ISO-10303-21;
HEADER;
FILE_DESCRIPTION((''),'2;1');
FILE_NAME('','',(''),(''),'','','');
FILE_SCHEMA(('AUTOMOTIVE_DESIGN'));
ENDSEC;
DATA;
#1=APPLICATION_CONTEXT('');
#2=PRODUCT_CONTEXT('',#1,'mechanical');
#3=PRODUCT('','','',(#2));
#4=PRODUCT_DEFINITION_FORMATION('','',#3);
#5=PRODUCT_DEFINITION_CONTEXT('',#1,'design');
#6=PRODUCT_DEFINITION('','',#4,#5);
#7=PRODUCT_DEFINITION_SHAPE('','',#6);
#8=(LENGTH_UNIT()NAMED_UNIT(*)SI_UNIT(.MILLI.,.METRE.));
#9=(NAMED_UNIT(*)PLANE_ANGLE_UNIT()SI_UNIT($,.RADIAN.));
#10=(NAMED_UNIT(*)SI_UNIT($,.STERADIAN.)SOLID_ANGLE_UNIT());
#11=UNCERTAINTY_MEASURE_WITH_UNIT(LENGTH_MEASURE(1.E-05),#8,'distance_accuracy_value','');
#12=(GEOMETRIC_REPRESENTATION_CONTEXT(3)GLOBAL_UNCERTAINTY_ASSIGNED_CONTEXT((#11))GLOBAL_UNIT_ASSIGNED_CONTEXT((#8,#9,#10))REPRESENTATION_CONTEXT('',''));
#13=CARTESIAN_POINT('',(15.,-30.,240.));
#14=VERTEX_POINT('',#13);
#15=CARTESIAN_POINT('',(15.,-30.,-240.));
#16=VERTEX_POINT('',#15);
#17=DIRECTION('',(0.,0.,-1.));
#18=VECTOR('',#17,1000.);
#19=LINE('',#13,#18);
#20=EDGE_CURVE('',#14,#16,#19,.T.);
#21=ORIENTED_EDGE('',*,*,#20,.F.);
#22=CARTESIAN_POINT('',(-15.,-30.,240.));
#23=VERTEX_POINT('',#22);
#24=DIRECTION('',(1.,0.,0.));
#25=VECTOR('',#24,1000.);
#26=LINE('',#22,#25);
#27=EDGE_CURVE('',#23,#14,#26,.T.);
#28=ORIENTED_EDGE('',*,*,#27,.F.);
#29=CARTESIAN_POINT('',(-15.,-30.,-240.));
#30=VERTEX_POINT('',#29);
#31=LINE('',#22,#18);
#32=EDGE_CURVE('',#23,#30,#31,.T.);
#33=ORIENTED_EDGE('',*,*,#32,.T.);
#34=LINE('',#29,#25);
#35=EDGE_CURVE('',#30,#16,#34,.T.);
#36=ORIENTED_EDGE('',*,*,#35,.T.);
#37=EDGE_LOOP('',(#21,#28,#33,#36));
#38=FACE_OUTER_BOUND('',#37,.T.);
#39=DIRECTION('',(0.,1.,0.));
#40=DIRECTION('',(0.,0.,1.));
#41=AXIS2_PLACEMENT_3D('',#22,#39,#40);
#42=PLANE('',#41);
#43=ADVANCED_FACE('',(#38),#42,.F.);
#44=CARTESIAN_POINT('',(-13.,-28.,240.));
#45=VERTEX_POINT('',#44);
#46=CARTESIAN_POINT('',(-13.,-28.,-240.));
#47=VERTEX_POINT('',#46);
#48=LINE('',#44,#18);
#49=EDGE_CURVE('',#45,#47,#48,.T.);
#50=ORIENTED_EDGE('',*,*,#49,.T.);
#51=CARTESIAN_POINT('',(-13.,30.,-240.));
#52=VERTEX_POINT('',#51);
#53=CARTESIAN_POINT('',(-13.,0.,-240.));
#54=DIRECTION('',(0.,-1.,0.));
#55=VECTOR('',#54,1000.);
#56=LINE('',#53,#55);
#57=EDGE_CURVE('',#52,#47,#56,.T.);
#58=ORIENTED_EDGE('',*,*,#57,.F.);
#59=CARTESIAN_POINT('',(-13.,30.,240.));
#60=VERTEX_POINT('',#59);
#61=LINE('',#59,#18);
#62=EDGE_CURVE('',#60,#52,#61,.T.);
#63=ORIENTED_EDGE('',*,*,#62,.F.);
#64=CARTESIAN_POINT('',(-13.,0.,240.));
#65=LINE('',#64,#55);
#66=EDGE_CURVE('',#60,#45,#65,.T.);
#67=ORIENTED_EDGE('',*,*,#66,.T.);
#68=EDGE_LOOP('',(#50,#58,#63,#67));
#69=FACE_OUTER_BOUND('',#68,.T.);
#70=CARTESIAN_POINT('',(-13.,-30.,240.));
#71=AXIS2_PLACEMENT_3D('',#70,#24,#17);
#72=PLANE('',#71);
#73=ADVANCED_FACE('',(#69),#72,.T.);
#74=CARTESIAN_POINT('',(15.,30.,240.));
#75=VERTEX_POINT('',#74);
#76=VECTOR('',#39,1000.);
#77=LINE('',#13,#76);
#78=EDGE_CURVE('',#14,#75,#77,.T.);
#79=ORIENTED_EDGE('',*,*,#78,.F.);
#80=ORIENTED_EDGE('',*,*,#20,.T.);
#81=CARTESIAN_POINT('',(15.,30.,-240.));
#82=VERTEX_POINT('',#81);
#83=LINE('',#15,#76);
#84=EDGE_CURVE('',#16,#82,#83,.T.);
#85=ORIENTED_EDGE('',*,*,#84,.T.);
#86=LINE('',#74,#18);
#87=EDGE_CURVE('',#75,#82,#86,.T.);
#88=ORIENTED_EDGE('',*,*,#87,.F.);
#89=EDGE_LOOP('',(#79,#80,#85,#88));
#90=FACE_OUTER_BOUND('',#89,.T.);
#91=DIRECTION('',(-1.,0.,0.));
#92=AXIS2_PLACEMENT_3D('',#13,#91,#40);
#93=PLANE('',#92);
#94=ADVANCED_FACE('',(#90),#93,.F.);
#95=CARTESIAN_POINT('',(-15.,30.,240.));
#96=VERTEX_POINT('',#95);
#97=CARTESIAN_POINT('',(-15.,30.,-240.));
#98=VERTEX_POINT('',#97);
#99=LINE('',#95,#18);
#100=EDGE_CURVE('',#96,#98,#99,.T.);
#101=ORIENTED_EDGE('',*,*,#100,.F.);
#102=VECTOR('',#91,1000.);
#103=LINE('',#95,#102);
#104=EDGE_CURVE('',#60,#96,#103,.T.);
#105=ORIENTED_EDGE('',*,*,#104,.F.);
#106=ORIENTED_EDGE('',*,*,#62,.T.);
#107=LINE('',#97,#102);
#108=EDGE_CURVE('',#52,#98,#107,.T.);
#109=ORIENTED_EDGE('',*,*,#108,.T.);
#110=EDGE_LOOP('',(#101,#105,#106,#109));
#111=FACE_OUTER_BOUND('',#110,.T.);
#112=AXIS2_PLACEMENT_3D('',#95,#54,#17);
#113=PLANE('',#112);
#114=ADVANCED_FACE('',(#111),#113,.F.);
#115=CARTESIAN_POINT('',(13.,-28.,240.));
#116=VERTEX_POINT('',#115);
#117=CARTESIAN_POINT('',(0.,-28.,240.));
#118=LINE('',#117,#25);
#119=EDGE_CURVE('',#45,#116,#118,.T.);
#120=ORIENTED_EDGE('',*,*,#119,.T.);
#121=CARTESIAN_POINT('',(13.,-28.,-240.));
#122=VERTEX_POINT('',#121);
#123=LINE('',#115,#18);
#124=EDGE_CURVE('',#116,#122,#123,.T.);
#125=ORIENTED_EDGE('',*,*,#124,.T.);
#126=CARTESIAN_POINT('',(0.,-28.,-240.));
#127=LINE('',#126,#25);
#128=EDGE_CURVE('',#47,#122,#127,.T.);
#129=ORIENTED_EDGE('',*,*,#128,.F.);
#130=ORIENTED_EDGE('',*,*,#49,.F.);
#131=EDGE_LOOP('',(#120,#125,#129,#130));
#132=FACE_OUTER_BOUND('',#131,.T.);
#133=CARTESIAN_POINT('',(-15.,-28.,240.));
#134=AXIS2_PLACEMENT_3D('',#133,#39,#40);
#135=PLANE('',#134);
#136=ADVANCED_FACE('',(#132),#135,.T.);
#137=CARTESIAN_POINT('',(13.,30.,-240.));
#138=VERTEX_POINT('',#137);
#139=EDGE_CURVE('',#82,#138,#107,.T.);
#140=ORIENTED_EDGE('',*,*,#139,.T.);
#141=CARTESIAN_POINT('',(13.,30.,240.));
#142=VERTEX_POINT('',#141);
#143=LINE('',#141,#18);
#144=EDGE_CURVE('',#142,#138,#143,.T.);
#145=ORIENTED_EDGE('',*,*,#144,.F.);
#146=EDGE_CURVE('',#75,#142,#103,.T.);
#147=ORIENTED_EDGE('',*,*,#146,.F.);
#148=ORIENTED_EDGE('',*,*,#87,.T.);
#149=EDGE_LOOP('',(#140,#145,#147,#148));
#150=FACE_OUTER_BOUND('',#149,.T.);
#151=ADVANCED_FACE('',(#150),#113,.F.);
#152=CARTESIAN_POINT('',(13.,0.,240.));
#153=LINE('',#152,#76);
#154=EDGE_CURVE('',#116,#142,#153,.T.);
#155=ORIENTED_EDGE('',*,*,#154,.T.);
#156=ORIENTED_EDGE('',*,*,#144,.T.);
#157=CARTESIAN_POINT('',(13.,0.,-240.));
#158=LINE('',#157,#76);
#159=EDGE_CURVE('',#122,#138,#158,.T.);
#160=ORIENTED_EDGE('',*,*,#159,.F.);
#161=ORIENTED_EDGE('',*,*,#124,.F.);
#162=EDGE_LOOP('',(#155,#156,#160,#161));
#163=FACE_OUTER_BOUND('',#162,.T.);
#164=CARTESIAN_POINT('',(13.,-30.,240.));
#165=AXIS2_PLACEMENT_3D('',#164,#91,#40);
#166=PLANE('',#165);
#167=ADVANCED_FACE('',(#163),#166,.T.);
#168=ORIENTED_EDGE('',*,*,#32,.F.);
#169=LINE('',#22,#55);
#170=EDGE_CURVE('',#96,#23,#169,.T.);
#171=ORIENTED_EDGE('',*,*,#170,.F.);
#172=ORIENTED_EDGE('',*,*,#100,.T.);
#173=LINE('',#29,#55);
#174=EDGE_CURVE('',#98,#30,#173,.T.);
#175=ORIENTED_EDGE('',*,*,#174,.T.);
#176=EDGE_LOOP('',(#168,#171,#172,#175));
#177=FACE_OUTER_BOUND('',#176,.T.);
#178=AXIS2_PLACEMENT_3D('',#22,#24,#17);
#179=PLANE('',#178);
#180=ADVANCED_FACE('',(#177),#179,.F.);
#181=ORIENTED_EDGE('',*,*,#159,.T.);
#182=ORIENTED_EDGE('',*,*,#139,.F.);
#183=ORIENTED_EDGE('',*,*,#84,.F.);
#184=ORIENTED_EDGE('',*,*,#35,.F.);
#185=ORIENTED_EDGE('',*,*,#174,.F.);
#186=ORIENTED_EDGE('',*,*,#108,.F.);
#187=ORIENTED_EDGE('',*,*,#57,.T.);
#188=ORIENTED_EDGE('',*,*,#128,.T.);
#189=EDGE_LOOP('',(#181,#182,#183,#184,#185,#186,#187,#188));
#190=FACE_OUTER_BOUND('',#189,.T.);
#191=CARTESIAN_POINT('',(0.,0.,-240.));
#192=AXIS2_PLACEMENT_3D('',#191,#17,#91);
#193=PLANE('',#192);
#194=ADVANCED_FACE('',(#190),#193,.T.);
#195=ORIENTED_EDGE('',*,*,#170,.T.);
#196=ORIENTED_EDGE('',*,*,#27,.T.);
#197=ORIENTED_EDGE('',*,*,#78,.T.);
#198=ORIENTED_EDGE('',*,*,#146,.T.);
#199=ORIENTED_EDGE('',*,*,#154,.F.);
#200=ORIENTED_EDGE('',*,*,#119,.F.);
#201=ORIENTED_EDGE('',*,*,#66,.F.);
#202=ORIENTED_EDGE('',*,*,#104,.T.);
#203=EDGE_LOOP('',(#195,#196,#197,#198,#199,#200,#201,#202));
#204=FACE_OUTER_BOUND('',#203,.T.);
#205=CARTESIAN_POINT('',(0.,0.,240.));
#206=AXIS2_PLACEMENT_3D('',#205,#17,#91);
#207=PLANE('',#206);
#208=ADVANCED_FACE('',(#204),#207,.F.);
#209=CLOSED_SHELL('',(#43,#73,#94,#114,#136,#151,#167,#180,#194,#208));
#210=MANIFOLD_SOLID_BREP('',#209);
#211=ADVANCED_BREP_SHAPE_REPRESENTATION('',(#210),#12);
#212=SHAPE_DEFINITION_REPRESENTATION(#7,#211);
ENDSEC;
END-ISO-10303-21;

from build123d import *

# Parameters (mm, degrees)
SKETCH_1_W      = 30
SKETCH_1_H      = 60
EXTRUDE_1_DEPTH = 240
SHELL_1_T       = -2


with BuildPart() as part:
    # 草图1 → 凸台-拉伸1 (new, symmetric)
    with BuildSketch(Plane.XY):
        Rectangle(SKETCH_1_W, SKETCH_1_H)
    extrude(amount=EXTRUDE_1_DEPTH, both=True)

    # 抽壳1
    shell_1_openings = [part.faces().sort_by_distance(p)[0] for p in [
        (0, 0, 240),
        (0, 0, -240),
        (0, 30, 0),
    ]]
    offset(amount=SHELL_1_T, openings=shell_1_openings, kind=Kind.INTERSECTION)


solid = part.part
